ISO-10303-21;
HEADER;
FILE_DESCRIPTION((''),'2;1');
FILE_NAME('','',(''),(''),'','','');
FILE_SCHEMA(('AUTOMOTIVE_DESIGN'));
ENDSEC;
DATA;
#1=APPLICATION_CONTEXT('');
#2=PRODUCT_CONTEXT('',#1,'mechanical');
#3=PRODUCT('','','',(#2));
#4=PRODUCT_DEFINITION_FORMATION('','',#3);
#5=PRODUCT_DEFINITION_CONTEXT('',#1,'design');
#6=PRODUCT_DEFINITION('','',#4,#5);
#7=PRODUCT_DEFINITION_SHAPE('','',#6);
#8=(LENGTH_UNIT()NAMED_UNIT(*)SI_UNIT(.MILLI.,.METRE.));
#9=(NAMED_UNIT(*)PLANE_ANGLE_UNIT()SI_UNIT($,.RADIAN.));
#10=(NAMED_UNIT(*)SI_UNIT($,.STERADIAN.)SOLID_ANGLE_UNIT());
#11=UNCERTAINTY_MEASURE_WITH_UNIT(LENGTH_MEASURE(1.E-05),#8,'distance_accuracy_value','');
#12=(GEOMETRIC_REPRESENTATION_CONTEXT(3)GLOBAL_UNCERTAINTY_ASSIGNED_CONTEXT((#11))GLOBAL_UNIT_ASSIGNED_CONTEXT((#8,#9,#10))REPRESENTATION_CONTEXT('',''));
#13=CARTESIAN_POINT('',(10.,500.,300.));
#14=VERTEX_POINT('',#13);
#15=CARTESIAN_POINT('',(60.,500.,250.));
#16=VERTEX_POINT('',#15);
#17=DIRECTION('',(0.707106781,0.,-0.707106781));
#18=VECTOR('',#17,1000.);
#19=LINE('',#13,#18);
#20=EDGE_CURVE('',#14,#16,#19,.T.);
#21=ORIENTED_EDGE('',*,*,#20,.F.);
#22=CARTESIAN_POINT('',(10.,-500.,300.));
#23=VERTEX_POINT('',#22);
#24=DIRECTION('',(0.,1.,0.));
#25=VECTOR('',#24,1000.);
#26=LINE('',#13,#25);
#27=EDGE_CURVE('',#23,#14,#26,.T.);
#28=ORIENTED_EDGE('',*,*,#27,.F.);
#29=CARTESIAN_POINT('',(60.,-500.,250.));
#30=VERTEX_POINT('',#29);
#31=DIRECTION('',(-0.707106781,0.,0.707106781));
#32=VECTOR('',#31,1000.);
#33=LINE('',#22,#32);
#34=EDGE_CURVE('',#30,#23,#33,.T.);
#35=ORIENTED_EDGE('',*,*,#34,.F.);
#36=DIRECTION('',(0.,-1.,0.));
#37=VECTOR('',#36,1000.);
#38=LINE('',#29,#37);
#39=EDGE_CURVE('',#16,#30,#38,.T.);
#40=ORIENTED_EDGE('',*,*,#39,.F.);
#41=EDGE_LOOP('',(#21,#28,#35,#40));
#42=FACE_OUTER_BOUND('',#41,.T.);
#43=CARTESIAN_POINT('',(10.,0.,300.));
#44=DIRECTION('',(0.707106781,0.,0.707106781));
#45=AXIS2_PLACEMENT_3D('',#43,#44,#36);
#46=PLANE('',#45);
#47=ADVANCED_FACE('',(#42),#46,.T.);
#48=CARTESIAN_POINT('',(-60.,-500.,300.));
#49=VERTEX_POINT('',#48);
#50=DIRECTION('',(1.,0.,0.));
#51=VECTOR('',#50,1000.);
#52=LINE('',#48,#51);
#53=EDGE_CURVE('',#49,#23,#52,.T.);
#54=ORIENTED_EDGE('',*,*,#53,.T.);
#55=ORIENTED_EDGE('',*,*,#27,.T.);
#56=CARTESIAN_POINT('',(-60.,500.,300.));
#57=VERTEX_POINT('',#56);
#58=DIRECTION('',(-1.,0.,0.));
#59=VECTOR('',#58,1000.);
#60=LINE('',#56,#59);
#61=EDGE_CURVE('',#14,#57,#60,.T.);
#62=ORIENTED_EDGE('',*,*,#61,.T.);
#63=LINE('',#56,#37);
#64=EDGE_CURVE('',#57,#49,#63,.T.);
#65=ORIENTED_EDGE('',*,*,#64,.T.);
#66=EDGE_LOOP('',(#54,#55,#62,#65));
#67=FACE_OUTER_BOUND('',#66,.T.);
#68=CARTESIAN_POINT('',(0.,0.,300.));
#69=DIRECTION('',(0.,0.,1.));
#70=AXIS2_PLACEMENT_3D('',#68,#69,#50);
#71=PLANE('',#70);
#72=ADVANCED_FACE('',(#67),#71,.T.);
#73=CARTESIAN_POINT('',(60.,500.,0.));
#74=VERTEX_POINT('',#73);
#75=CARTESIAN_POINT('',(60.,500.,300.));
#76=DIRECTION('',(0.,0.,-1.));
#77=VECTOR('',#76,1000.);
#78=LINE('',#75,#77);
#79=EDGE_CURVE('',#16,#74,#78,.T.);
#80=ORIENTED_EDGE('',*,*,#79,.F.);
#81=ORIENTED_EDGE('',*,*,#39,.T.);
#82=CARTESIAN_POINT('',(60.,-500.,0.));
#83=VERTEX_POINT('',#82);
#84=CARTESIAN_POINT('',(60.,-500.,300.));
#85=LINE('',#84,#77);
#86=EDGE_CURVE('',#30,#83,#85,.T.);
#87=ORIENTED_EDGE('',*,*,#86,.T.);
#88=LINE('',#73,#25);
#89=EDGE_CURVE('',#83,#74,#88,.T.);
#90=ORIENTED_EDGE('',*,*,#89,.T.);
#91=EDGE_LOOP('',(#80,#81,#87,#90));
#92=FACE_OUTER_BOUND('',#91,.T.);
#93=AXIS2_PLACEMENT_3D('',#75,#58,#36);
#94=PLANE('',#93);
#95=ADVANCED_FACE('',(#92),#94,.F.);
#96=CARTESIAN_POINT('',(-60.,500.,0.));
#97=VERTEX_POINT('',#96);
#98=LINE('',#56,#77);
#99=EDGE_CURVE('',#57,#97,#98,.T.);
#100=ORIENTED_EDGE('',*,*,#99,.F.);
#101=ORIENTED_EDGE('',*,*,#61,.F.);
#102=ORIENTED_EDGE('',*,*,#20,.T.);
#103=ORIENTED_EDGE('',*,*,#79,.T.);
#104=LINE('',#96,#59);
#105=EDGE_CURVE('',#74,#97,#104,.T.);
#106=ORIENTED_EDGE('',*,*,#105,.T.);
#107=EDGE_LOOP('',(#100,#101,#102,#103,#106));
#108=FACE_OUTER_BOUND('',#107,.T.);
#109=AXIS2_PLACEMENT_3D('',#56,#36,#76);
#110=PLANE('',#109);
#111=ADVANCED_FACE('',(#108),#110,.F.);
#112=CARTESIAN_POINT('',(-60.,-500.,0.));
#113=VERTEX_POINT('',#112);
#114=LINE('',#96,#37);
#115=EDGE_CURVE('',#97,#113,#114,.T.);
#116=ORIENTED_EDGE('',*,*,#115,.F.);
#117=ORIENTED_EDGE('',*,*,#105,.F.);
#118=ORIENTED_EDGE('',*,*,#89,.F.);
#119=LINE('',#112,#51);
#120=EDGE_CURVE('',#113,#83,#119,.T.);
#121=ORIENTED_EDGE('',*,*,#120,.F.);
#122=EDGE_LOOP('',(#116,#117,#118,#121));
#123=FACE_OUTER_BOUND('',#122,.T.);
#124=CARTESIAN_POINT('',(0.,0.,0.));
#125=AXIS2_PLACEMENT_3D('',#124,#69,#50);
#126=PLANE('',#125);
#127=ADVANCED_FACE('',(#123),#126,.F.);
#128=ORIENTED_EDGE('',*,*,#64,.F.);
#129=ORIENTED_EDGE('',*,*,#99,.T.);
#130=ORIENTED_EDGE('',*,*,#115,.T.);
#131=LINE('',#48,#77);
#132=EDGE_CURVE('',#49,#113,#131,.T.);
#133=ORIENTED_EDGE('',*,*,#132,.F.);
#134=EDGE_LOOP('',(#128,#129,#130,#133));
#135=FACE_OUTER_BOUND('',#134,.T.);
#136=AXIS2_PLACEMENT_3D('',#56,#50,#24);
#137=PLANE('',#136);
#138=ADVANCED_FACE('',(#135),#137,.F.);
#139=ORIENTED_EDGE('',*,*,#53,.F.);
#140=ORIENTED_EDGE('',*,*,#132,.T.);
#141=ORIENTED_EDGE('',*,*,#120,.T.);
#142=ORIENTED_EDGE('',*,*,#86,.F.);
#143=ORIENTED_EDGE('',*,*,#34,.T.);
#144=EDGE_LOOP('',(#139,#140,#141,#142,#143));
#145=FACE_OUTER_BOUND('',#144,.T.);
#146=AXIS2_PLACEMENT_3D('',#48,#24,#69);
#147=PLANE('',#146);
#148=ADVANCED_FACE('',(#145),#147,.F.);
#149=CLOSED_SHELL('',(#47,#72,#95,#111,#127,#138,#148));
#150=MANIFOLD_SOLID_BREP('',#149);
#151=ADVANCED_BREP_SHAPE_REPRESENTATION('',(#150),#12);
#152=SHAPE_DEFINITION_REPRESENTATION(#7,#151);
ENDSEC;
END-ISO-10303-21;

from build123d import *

# Parameters (mm, degrees)
SKETCH1_W           = 120
SKETCH1_H           = 1000
BOSS_EXTRUDE1_DEPTH = 300
CHAMFER1_SIZE       = 50


with BuildPart() as part:
    # Sketch1 → Boss-Extrude1 (new body)
    with BuildSketch(Plane.XY):
        Rectangle(SKETCH1_W, SKETCH1_H)
    extrude(amount=BOSS_EXTRUDE1_DEPTH)

    # Chamfer1
    chamfer1_edges = [part.edges().sort_by_distance(p)[0] for p in [
        (60, 0, 300),
    ]]
    chamfer(chamfer1_edges, length=CHAMFER1_SIZE)


solid = part.part
